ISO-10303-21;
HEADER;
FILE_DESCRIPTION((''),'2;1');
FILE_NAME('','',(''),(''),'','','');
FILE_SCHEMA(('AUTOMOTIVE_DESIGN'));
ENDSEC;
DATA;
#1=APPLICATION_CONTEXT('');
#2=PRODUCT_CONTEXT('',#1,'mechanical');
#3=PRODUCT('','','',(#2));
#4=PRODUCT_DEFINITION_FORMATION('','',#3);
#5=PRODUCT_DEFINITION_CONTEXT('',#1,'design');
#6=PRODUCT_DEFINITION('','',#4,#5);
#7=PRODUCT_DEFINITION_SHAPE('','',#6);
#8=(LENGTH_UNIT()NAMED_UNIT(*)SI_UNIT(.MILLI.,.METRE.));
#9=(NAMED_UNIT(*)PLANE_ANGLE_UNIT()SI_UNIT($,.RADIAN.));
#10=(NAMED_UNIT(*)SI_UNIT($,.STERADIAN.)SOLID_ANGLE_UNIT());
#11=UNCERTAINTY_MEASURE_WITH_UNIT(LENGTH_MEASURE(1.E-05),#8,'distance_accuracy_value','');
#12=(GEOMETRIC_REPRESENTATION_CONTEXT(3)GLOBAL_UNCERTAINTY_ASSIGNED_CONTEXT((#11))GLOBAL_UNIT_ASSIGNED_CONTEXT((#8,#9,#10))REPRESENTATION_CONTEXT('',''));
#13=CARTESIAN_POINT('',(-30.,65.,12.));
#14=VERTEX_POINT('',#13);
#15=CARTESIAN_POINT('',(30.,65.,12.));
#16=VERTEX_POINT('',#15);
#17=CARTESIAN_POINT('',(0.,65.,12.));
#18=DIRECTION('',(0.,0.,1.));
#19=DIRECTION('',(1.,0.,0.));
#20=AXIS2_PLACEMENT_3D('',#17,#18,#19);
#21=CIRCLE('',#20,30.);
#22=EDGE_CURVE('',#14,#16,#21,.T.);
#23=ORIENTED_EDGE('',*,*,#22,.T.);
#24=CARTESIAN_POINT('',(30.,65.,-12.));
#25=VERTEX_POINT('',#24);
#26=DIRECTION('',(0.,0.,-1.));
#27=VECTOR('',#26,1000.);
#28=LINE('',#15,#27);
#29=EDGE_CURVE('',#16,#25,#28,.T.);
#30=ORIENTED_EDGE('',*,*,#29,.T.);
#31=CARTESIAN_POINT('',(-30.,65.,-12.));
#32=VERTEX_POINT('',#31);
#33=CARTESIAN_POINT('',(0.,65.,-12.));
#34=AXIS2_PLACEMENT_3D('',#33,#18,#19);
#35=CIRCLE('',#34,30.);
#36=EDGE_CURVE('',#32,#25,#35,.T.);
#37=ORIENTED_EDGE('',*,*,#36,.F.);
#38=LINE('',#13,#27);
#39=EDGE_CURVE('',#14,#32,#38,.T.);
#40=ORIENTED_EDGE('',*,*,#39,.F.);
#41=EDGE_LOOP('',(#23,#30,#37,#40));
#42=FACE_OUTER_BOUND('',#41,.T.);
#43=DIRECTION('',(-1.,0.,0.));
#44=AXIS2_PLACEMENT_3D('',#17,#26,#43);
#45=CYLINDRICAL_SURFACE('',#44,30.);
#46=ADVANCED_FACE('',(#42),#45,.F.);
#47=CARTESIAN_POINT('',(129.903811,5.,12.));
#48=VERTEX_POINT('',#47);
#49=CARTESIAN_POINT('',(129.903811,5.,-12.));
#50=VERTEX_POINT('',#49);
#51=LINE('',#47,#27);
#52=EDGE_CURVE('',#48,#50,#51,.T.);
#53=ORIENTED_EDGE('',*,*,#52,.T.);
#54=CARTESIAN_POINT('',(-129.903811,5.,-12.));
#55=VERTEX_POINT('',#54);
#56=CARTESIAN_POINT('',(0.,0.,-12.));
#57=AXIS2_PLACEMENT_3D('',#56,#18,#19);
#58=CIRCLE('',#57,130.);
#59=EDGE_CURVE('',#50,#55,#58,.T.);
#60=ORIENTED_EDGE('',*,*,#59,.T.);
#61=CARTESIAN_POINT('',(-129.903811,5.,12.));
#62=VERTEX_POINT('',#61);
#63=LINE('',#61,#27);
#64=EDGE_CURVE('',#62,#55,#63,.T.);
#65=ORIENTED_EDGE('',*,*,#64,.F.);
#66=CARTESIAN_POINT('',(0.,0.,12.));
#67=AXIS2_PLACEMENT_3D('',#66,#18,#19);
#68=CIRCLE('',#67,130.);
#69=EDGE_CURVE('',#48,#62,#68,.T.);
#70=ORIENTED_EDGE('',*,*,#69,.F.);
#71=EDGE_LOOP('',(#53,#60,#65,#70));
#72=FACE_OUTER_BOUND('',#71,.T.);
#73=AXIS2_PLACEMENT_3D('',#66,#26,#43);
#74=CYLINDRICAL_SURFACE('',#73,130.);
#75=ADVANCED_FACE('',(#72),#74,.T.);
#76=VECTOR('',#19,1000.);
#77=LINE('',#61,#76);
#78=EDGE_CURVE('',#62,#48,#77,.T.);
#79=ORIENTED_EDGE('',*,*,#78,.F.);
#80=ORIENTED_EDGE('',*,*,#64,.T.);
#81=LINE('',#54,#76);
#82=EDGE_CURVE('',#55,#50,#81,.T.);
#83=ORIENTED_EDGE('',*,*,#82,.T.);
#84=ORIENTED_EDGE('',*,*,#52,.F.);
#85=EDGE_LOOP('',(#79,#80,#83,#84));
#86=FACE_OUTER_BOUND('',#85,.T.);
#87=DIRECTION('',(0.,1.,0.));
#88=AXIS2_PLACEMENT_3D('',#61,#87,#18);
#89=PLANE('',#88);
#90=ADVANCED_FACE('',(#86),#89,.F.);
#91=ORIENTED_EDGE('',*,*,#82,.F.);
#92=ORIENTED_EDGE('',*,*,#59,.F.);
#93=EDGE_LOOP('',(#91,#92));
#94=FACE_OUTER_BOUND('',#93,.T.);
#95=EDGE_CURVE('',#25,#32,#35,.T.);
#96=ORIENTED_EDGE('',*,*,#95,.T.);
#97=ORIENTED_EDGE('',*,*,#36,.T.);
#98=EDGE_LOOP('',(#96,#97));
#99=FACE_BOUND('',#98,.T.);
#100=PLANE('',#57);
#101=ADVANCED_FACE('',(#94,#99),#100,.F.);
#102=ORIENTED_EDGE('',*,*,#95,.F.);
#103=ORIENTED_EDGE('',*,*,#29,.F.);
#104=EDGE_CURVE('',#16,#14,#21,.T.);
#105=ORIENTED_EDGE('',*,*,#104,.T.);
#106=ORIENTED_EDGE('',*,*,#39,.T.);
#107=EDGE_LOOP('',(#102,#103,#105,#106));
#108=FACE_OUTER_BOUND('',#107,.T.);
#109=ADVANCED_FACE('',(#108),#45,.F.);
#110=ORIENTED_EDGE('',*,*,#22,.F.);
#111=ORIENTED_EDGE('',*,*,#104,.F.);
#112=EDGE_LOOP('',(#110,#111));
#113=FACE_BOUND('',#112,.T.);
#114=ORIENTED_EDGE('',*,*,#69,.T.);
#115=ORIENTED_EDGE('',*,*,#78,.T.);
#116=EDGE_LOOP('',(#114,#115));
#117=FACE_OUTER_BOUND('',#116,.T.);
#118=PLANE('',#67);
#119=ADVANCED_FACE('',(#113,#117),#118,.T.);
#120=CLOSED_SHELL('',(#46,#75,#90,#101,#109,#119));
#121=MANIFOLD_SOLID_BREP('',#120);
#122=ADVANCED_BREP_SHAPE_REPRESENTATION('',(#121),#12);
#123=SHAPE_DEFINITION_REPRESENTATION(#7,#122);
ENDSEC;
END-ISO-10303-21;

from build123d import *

# Parameters (mm, degrees)
SKETCH1_R           = 30
BOSS_EXTRUDE1_DEPTH = 12


with BuildPart() as part:
    # Sketch1 → Boss-Extrude1 (new, symmetric)
    with BuildSketch(Plane.XY):
        with BuildLine():
            Line((-129.903810568, 5), (129.903810568, 5))
            ThreePointArc((129.903810568, 5), (0, 130), (-129.903810568, 5))
        make_face()
        with Locations((0, 65)):
            Circle(SKETCH1_R, mode=Mode.SUBTRACT)
    extrude(amount=BOSS_EXTRUDE1_DEPTH, both=True)


solid = part.part
